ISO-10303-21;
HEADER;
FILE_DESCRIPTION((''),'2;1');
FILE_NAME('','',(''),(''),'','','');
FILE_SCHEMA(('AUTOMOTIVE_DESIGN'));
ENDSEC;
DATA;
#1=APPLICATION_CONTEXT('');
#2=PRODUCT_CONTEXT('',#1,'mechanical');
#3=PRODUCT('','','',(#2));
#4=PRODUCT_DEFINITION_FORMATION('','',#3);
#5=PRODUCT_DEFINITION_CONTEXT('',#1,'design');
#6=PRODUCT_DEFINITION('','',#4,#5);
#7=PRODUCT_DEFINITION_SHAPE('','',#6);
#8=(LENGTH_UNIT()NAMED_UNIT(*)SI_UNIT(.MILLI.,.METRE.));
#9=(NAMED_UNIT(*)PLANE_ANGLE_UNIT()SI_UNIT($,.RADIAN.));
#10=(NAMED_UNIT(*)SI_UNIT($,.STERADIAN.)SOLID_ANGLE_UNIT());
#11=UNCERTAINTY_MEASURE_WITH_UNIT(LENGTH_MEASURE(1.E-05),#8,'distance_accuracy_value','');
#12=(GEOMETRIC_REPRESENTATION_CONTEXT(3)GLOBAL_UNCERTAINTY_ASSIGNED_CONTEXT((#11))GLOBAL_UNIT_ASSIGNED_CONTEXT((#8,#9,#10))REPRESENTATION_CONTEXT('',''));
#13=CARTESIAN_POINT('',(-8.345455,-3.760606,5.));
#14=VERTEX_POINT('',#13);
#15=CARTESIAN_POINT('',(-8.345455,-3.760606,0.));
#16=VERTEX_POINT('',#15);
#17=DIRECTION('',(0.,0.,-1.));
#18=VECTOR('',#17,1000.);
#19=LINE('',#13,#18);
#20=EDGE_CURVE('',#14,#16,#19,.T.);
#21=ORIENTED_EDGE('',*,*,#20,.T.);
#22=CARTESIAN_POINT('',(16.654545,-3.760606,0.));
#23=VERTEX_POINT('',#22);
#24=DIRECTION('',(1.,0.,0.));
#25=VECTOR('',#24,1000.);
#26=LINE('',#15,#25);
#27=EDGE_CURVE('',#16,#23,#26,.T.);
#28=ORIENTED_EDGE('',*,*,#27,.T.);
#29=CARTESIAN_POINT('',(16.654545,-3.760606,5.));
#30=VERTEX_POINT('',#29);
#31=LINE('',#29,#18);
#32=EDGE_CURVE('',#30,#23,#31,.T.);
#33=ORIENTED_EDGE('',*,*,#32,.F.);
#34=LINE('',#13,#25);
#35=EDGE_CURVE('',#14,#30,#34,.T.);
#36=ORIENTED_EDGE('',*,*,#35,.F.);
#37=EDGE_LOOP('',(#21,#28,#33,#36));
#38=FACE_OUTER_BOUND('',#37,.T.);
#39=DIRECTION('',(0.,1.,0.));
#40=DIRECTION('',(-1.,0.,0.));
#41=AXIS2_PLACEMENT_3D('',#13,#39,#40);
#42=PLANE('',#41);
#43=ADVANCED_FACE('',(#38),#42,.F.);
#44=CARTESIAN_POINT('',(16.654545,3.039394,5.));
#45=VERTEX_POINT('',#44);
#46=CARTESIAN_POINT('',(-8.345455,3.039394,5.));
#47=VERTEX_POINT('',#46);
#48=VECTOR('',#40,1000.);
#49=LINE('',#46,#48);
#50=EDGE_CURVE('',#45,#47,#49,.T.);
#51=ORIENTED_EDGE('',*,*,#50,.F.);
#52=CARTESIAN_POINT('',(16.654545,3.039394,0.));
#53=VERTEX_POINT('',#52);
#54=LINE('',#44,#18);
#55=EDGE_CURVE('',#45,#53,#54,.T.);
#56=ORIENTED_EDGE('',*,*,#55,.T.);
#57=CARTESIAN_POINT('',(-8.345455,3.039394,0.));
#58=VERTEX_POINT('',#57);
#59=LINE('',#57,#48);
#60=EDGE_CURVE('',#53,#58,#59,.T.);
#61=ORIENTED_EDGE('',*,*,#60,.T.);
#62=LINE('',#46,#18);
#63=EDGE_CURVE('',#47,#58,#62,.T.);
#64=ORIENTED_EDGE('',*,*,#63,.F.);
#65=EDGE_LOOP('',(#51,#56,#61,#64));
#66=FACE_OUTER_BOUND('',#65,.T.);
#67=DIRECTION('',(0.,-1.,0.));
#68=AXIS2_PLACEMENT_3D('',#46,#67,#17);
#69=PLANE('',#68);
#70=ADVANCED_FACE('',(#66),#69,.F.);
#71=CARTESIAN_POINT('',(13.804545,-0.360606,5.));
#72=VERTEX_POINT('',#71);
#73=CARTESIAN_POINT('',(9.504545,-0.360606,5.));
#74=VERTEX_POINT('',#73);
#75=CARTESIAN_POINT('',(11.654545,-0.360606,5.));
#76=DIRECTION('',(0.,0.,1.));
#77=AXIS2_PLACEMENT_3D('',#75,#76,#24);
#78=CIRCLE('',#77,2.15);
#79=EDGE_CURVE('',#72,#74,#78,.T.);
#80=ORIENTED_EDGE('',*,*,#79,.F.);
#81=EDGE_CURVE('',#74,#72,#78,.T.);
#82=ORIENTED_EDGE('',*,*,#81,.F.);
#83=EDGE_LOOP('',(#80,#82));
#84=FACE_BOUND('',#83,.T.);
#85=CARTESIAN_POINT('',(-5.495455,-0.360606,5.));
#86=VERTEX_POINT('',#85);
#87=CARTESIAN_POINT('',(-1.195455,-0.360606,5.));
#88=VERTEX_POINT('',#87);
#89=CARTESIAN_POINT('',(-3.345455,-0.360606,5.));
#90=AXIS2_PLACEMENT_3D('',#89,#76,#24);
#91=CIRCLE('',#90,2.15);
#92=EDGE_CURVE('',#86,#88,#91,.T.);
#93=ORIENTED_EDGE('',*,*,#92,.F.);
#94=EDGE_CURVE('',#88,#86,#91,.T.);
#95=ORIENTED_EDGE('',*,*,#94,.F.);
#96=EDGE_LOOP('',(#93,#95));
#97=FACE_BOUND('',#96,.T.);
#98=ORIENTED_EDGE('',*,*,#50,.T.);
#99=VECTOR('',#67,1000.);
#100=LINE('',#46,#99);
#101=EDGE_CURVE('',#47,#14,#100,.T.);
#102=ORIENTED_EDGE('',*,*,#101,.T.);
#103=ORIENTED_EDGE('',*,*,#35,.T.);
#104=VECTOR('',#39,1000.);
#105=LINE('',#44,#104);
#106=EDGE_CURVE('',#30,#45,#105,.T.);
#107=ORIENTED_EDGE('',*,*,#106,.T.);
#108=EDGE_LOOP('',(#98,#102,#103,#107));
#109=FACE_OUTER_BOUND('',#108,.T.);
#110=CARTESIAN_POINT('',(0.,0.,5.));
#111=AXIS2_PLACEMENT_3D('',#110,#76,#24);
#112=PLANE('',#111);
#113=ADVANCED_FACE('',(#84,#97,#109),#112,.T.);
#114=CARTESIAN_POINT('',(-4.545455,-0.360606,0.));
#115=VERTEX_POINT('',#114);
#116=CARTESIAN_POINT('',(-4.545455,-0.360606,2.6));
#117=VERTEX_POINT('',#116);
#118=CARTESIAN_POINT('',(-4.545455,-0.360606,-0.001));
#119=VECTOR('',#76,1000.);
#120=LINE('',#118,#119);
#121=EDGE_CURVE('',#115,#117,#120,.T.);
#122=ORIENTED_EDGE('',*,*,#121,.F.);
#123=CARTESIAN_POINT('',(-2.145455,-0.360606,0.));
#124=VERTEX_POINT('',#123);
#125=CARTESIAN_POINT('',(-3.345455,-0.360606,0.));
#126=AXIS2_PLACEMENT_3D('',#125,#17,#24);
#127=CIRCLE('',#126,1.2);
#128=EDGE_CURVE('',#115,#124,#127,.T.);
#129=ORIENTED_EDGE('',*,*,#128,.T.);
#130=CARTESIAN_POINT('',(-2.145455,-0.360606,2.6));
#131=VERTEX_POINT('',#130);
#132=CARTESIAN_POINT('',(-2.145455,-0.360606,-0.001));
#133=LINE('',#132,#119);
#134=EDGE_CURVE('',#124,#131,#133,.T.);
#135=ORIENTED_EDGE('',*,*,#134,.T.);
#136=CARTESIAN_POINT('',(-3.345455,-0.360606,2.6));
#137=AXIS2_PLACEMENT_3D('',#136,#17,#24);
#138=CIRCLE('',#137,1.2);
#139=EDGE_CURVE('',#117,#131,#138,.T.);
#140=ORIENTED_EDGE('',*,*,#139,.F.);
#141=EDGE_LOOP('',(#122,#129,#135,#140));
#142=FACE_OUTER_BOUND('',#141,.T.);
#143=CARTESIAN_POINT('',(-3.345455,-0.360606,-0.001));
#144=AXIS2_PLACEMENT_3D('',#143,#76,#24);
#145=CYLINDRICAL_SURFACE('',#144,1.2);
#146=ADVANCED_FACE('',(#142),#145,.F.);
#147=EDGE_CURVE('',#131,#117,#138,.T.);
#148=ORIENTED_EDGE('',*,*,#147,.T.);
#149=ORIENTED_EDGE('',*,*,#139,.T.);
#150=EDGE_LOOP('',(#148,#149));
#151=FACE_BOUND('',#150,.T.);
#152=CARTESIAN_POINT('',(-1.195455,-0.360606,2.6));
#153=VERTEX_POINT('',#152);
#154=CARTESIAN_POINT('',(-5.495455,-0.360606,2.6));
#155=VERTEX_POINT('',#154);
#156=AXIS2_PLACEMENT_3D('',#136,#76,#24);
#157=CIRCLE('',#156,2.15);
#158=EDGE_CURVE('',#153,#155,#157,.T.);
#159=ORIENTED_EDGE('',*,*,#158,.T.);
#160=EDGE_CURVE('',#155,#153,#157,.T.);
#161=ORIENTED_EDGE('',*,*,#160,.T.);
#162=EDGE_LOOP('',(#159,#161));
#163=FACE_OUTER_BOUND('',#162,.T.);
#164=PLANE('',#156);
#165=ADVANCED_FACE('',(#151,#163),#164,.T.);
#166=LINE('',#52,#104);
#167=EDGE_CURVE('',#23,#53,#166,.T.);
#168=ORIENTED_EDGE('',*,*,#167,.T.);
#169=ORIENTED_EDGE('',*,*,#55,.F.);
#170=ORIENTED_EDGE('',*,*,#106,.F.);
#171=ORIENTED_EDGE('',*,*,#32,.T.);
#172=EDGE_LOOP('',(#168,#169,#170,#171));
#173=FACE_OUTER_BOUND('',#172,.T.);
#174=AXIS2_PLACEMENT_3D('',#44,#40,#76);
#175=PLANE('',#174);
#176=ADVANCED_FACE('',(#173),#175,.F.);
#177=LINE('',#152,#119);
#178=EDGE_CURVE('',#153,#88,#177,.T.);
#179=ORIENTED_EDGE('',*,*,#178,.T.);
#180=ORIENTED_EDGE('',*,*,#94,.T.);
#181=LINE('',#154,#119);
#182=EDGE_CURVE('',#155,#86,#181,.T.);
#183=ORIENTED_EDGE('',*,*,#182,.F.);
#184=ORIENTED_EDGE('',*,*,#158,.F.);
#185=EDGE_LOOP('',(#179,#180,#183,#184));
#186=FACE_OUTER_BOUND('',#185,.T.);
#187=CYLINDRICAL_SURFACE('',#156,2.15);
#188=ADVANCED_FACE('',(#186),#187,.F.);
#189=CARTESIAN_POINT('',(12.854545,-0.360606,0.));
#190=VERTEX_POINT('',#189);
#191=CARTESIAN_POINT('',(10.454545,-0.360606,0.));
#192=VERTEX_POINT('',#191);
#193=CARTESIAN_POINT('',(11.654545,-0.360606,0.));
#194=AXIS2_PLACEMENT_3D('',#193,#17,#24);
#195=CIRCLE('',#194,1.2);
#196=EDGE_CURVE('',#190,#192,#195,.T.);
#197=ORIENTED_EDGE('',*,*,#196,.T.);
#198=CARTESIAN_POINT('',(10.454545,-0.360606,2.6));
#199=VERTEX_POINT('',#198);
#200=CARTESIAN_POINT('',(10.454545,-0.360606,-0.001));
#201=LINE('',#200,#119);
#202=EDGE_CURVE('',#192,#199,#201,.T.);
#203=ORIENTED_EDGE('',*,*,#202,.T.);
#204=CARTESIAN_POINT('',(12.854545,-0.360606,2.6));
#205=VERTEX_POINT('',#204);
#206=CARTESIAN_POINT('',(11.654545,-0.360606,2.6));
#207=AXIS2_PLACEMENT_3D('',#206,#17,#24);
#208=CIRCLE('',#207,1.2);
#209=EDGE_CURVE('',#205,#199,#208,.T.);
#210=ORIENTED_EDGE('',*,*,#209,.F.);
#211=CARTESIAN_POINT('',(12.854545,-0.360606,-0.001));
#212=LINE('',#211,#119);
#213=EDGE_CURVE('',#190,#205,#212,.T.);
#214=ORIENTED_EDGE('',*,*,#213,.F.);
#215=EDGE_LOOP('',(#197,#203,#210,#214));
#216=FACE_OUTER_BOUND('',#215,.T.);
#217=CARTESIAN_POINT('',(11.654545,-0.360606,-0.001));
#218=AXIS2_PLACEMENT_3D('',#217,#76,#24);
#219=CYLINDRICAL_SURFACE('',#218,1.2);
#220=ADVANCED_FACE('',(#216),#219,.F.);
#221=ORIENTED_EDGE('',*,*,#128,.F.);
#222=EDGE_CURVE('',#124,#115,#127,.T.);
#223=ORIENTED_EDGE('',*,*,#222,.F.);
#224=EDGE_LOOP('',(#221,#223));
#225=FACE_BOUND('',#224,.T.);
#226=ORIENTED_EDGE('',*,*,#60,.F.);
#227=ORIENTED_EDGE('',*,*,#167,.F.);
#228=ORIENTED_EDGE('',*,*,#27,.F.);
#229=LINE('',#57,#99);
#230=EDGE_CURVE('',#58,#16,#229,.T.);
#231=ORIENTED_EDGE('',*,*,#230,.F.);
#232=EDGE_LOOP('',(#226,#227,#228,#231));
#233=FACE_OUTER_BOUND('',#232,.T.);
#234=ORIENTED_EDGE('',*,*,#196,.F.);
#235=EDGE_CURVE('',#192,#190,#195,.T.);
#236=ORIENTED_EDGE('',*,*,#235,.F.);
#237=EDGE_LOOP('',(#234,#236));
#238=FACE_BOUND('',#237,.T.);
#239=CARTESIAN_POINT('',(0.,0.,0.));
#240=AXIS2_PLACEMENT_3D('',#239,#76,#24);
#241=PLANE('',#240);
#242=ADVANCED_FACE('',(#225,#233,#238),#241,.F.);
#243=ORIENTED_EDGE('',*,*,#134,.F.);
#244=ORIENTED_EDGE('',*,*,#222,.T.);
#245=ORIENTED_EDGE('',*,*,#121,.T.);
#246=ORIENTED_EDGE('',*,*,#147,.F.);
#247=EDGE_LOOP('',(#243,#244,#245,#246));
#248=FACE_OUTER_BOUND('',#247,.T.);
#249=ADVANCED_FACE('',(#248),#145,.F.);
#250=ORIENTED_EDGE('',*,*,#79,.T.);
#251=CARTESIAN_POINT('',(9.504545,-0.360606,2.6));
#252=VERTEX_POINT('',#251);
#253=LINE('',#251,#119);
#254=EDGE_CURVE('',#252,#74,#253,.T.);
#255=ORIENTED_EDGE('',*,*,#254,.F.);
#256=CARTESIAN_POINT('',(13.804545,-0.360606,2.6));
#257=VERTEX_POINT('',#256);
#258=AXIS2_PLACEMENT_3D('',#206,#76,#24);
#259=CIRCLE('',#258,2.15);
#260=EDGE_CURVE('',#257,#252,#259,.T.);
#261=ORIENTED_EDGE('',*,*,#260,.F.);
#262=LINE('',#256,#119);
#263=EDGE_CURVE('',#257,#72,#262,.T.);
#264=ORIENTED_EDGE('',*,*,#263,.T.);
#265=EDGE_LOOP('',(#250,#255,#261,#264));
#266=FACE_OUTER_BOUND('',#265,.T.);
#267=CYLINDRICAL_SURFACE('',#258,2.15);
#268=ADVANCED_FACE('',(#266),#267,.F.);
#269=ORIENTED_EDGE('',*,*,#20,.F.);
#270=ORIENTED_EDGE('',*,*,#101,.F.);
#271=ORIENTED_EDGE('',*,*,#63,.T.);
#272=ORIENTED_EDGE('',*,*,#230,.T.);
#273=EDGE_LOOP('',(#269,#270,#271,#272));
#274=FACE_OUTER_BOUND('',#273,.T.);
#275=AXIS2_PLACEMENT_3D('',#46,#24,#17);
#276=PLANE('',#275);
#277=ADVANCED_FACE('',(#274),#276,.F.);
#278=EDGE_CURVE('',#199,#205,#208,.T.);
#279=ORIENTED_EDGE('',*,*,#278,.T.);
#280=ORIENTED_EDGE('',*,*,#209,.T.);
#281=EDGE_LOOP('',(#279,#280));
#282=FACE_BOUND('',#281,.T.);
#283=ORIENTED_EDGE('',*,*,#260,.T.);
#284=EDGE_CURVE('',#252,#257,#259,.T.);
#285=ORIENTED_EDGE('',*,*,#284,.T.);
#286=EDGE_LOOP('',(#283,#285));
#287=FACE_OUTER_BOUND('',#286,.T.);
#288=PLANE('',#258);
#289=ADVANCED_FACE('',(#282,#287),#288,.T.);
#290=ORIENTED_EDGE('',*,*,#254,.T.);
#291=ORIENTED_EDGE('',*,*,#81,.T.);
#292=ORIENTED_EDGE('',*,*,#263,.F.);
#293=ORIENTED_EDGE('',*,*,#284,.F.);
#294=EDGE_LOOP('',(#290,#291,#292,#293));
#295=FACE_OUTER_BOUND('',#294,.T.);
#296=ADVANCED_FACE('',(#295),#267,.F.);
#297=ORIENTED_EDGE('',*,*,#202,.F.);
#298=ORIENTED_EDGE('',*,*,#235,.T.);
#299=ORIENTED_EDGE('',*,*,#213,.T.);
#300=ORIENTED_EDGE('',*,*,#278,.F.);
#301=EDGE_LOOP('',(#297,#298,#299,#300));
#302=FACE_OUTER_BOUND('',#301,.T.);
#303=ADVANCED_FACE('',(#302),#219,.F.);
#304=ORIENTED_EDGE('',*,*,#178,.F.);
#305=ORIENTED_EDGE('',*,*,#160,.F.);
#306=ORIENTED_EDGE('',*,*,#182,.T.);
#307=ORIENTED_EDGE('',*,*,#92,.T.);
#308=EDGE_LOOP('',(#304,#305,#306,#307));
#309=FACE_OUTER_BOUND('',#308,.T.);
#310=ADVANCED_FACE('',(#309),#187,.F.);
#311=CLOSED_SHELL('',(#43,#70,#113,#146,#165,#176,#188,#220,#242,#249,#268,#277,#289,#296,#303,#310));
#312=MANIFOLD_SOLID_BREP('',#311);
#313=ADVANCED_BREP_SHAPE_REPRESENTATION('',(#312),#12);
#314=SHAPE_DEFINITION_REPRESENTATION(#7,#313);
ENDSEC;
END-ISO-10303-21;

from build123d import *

# Parameters (mm, degrees)
SKETCH_1_W          = 25
SKETCH_1_H          = 6.8
EXTRUDE_1_DEPTH     = 5
CUT_EXTRUDE_1_REACH = 19.791
SKETCH_2_R          = 1.2
SKETCH_3_R          = 2.15
CUT_EXTRUDE_2_DEPTH = 2.4


with BuildPart() as part:
    # 草图1 → 凸台-拉伸1 (new body)
    with BuildSketch(Plane.XY):
        with Locations((4.154545455, -0.360606061)):
            Rectangle(SKETCH_1_W, SKETCH_1_H)
    extrude(amount=EXTRUDE_1_DEPTH)

    # 草图2 → 切除-拉伸1 (cut, up to next)
    with BuildSketch(Plane.XY.offset(5), mode=Mode.PRIVATE) as cut_extrude_1_sk1:
        with Locations((-3.345454545, -0.360606061)):
            Circle(SKETCH_2_R)
    cut_extrude_1_tool1 = extrude(cut_extrude_1_sk1.sketch, amount=-CUT_EXTRUDE_1_REACH, mode=Mode.PRIVATE) & part.part
    # 草图2 → 切除-拉伸1 (cut, up to next)
    with BuildSketch(Plane.XY.offset(5), mode=Mode.PRIVATE) as cut_extrude_1_sk2:
        with Locations((11.654545455, -0.360606061)):
            Circle(SKETCH_2_R)
    cut_extrude_1_tool2 = extrude(cut_extrude_1_sk2.sketch, amount=-CUT_EXTRUDE_1_REACH, mode=Mode.PRIVATE) & part.part
    add(cut_extrude_1_tool1.solids().sort_by_distance((-3.345455, -0.360606, 5))[0], mode=Mode.SUBTRACT)
    add(cut_extrude_1_tool2.solids().sort_by_distance((11.654545, -0.360606, 5))[0], mode=Mode.SUBTRACT)

    # 草图3 → 切除-拉伸2 (cut)
    with BuildSketch(Plane.XY.offset(5)):
        with Locations((-3.345454545, -0.360606061)):
            Circle(SKETCH_3_R)
        with Locations((11.654545455, -0.360606061)):
            Circle(SKETCH_3_R)
    extrude(amount=-CUT_EXTRUDE_2_DEPTH, mode=Mode.SUBTRACT)


solid = part.part
